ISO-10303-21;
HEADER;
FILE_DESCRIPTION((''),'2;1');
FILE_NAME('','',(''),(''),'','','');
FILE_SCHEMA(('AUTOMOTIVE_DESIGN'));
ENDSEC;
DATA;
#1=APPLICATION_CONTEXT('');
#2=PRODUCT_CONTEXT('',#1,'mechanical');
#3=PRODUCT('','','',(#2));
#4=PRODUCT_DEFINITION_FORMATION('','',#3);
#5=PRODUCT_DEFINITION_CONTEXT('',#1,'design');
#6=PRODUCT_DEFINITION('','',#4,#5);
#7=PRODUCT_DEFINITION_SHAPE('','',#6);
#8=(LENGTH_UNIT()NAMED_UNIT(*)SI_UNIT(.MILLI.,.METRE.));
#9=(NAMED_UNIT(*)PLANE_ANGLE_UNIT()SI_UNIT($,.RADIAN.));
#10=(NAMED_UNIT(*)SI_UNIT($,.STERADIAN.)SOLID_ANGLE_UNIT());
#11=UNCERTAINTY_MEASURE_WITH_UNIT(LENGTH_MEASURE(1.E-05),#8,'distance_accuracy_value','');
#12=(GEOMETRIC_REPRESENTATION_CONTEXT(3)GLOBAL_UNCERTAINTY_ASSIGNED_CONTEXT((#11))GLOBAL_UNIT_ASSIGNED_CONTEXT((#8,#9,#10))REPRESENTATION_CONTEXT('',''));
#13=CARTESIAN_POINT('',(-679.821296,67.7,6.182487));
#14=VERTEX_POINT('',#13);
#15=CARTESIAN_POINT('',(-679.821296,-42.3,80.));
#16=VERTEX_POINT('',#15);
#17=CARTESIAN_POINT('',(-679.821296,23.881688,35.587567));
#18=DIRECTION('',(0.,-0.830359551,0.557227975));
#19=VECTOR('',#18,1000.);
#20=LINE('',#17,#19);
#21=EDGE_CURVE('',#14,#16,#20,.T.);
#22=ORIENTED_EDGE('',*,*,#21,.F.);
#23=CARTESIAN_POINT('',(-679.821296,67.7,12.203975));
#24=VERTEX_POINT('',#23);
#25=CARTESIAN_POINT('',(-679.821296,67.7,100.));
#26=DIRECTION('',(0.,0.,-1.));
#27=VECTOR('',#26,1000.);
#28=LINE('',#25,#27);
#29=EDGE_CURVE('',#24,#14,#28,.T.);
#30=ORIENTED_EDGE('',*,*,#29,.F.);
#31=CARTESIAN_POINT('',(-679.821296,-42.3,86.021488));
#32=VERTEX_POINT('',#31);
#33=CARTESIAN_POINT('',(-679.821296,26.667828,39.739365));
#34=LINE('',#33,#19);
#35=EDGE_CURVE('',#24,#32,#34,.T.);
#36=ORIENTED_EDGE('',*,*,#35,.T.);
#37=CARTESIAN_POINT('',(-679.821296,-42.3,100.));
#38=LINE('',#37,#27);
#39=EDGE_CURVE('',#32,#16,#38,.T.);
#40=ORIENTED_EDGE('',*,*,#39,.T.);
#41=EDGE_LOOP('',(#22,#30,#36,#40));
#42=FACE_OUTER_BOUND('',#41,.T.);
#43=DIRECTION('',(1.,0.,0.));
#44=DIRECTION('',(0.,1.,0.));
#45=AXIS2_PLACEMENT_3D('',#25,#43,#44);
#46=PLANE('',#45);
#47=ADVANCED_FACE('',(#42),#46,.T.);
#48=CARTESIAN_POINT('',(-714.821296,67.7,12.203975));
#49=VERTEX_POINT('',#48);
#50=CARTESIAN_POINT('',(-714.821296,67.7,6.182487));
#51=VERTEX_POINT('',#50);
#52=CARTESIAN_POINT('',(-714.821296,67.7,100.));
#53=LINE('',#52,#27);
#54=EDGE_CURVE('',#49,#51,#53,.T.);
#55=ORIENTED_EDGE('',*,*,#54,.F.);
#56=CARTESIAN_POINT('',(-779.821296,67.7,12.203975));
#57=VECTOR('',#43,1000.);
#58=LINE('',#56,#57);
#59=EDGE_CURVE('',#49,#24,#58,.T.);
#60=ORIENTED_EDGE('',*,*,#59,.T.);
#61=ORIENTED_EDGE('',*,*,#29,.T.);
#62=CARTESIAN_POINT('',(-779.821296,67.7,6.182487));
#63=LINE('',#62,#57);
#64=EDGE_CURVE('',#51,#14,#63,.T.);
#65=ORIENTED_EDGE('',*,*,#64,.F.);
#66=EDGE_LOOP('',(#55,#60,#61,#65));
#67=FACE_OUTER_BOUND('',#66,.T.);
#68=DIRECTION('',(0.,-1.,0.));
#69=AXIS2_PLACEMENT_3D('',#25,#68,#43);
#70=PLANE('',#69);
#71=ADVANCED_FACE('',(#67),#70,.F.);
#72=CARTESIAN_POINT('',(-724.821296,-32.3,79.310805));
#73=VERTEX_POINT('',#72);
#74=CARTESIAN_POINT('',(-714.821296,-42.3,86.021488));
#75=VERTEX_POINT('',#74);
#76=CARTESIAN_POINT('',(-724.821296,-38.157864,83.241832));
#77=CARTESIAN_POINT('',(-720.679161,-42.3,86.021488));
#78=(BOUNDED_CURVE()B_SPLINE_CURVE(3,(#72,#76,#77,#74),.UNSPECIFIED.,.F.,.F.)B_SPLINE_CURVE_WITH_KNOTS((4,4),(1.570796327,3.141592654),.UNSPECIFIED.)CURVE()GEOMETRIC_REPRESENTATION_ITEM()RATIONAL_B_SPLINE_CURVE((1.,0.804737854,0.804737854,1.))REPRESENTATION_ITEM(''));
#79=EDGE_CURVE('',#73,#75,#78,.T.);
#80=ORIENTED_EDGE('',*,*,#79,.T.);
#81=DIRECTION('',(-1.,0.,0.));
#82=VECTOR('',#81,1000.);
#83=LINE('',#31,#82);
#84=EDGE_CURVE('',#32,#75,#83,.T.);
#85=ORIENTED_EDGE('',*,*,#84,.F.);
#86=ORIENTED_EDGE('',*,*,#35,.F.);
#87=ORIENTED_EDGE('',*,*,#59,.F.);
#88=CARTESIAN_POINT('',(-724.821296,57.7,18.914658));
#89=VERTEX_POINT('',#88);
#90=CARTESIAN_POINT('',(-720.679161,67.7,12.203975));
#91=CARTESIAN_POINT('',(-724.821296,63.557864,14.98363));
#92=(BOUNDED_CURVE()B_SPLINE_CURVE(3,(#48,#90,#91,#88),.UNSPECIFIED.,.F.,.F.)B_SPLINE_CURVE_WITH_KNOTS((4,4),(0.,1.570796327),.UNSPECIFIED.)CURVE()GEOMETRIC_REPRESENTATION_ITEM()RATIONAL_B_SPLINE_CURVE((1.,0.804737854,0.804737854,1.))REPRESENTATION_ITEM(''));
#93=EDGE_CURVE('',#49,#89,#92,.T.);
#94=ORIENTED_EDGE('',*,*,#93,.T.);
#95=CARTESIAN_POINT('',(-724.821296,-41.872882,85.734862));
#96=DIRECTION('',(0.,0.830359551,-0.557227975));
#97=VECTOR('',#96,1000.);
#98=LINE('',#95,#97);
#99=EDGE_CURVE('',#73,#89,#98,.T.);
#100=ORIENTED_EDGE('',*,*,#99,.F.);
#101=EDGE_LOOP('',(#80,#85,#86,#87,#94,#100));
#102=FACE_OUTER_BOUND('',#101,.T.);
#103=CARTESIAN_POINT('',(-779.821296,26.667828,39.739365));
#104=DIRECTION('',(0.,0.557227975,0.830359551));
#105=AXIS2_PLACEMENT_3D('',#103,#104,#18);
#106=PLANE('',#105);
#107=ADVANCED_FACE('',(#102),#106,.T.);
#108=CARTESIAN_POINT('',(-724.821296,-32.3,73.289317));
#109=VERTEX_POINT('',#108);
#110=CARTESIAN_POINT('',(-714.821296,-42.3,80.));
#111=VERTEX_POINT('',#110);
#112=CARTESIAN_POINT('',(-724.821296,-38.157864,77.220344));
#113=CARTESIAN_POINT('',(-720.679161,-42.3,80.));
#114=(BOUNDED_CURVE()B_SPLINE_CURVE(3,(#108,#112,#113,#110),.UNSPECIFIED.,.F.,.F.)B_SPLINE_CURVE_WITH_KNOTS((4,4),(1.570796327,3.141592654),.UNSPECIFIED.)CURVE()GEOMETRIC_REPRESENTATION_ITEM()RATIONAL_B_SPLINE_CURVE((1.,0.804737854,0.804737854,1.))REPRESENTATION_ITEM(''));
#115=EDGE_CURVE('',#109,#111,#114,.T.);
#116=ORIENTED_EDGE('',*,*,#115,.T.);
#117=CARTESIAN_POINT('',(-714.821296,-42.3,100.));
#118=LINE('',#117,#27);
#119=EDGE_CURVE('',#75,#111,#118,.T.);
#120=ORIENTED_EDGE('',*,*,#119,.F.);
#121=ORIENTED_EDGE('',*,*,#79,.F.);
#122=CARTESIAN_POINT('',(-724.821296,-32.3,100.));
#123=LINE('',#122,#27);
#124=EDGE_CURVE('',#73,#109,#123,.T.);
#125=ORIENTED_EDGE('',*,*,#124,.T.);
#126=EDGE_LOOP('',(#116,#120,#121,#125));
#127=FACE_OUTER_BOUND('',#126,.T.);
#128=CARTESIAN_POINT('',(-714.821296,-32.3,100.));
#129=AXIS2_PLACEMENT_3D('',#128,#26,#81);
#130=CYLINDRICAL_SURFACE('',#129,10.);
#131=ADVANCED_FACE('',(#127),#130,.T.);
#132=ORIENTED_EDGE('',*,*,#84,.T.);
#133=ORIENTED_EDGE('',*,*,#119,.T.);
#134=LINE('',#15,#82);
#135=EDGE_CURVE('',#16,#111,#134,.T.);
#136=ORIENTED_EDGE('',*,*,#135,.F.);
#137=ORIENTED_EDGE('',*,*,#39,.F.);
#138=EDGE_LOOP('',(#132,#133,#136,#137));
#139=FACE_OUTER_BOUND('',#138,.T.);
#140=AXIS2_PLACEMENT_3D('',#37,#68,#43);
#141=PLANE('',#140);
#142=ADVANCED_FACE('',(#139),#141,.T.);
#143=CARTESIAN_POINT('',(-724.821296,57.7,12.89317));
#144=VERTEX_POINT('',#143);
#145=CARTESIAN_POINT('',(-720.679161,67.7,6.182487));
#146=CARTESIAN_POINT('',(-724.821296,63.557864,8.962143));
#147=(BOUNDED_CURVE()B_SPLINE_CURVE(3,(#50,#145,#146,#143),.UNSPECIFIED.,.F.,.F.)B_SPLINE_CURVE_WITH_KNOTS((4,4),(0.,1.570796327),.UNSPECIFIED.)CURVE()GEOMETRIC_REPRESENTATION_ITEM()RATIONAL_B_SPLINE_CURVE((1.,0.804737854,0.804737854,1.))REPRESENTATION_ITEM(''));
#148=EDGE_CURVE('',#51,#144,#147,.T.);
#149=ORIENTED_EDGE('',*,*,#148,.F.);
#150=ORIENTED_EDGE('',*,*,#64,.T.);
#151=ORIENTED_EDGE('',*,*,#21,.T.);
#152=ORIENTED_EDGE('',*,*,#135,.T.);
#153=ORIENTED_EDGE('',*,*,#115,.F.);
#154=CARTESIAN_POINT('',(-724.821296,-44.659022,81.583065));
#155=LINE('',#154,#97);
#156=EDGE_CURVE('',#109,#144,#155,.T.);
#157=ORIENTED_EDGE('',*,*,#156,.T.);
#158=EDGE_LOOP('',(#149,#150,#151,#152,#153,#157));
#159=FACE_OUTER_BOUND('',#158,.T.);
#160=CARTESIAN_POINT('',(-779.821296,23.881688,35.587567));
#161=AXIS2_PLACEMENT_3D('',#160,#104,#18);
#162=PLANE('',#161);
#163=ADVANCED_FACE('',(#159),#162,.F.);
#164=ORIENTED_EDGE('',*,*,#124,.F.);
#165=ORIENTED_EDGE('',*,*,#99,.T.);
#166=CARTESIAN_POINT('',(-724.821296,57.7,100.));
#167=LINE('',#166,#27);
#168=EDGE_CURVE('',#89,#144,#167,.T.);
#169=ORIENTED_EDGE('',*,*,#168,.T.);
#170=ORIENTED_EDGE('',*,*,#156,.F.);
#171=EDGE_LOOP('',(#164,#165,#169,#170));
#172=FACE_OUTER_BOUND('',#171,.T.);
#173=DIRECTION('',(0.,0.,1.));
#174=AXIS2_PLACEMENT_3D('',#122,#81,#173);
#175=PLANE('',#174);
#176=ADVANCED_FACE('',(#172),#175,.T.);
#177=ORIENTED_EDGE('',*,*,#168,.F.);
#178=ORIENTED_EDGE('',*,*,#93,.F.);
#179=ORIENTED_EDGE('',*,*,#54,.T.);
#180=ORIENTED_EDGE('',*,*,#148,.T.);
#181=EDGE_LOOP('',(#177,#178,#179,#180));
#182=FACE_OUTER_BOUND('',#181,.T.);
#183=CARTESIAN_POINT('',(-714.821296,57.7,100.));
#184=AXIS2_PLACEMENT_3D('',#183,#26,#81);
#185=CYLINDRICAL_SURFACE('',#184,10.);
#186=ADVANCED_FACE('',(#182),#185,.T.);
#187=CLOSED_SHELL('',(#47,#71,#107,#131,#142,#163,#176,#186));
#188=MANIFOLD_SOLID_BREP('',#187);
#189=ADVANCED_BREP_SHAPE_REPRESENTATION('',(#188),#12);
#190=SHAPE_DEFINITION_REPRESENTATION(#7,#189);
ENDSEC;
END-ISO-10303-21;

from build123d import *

# Parameters (mm, degrees)
EXTRUDE_2_DEPTH     = 100
SKETCH_3_OUTSIDE_W  = 133.064
SKETCH_3_OUTSIDE_H  = 143.064
CUT_EXTRUDE_5_DEPTH = 100


with BuildPart() as part:
    # 草图1 → 凸台-拉伸2 (new body)
    with BuildSketch(Plane.XY):
        with BuildLine():
            Line((-679.821296296, 67.7), (-679.821296296, -42.3))
            Line((-679.821296296, -42.3), (-714.821296296, -42.3))
            ThreePointArc((-714.821296296, -42.3), (-721.892364108, -39.371067812), (-724.821296296, -32.3))
            Line((-724.821296296, -32.3), (-724.821296296, 57.7))
            ThreePointArc((-724.821296296, 57.7), (-721.892364108, 64.771067812), (-714.821296296, 67.7))
            Line((-714.821296296, 67.7), (-679.821296296, 67.7))
        make_face()
    extrude(amount=EXTRUDE_2_DEPTH)

    # 草图3 outside → 切除-拉伸5 (cut)
    with BuildSketch(Plane(origin=(-679.821296296, 0, 0), x_dir=(0, 0, -1), z_dir=(1, 0, 0))):
        with Locations((-50, 12.7)):
            Rectangle(SKETCH_3_OUTSIDE_W, SKETCH_3_OUTSIDE_H)
        Polygon((-86.021487915, -42.3), (-80, -42.3), (-6.182486595, 67.7), (-12.203974509, 67.7), (-84.151797754, -39.513860124), align=None, mode=Mode.SUBTRACT)
    extrude(amount=-CUT_EXTRUDE_5_DEPTH, mode=Mode.SUBTRACT)


solid = part.part
